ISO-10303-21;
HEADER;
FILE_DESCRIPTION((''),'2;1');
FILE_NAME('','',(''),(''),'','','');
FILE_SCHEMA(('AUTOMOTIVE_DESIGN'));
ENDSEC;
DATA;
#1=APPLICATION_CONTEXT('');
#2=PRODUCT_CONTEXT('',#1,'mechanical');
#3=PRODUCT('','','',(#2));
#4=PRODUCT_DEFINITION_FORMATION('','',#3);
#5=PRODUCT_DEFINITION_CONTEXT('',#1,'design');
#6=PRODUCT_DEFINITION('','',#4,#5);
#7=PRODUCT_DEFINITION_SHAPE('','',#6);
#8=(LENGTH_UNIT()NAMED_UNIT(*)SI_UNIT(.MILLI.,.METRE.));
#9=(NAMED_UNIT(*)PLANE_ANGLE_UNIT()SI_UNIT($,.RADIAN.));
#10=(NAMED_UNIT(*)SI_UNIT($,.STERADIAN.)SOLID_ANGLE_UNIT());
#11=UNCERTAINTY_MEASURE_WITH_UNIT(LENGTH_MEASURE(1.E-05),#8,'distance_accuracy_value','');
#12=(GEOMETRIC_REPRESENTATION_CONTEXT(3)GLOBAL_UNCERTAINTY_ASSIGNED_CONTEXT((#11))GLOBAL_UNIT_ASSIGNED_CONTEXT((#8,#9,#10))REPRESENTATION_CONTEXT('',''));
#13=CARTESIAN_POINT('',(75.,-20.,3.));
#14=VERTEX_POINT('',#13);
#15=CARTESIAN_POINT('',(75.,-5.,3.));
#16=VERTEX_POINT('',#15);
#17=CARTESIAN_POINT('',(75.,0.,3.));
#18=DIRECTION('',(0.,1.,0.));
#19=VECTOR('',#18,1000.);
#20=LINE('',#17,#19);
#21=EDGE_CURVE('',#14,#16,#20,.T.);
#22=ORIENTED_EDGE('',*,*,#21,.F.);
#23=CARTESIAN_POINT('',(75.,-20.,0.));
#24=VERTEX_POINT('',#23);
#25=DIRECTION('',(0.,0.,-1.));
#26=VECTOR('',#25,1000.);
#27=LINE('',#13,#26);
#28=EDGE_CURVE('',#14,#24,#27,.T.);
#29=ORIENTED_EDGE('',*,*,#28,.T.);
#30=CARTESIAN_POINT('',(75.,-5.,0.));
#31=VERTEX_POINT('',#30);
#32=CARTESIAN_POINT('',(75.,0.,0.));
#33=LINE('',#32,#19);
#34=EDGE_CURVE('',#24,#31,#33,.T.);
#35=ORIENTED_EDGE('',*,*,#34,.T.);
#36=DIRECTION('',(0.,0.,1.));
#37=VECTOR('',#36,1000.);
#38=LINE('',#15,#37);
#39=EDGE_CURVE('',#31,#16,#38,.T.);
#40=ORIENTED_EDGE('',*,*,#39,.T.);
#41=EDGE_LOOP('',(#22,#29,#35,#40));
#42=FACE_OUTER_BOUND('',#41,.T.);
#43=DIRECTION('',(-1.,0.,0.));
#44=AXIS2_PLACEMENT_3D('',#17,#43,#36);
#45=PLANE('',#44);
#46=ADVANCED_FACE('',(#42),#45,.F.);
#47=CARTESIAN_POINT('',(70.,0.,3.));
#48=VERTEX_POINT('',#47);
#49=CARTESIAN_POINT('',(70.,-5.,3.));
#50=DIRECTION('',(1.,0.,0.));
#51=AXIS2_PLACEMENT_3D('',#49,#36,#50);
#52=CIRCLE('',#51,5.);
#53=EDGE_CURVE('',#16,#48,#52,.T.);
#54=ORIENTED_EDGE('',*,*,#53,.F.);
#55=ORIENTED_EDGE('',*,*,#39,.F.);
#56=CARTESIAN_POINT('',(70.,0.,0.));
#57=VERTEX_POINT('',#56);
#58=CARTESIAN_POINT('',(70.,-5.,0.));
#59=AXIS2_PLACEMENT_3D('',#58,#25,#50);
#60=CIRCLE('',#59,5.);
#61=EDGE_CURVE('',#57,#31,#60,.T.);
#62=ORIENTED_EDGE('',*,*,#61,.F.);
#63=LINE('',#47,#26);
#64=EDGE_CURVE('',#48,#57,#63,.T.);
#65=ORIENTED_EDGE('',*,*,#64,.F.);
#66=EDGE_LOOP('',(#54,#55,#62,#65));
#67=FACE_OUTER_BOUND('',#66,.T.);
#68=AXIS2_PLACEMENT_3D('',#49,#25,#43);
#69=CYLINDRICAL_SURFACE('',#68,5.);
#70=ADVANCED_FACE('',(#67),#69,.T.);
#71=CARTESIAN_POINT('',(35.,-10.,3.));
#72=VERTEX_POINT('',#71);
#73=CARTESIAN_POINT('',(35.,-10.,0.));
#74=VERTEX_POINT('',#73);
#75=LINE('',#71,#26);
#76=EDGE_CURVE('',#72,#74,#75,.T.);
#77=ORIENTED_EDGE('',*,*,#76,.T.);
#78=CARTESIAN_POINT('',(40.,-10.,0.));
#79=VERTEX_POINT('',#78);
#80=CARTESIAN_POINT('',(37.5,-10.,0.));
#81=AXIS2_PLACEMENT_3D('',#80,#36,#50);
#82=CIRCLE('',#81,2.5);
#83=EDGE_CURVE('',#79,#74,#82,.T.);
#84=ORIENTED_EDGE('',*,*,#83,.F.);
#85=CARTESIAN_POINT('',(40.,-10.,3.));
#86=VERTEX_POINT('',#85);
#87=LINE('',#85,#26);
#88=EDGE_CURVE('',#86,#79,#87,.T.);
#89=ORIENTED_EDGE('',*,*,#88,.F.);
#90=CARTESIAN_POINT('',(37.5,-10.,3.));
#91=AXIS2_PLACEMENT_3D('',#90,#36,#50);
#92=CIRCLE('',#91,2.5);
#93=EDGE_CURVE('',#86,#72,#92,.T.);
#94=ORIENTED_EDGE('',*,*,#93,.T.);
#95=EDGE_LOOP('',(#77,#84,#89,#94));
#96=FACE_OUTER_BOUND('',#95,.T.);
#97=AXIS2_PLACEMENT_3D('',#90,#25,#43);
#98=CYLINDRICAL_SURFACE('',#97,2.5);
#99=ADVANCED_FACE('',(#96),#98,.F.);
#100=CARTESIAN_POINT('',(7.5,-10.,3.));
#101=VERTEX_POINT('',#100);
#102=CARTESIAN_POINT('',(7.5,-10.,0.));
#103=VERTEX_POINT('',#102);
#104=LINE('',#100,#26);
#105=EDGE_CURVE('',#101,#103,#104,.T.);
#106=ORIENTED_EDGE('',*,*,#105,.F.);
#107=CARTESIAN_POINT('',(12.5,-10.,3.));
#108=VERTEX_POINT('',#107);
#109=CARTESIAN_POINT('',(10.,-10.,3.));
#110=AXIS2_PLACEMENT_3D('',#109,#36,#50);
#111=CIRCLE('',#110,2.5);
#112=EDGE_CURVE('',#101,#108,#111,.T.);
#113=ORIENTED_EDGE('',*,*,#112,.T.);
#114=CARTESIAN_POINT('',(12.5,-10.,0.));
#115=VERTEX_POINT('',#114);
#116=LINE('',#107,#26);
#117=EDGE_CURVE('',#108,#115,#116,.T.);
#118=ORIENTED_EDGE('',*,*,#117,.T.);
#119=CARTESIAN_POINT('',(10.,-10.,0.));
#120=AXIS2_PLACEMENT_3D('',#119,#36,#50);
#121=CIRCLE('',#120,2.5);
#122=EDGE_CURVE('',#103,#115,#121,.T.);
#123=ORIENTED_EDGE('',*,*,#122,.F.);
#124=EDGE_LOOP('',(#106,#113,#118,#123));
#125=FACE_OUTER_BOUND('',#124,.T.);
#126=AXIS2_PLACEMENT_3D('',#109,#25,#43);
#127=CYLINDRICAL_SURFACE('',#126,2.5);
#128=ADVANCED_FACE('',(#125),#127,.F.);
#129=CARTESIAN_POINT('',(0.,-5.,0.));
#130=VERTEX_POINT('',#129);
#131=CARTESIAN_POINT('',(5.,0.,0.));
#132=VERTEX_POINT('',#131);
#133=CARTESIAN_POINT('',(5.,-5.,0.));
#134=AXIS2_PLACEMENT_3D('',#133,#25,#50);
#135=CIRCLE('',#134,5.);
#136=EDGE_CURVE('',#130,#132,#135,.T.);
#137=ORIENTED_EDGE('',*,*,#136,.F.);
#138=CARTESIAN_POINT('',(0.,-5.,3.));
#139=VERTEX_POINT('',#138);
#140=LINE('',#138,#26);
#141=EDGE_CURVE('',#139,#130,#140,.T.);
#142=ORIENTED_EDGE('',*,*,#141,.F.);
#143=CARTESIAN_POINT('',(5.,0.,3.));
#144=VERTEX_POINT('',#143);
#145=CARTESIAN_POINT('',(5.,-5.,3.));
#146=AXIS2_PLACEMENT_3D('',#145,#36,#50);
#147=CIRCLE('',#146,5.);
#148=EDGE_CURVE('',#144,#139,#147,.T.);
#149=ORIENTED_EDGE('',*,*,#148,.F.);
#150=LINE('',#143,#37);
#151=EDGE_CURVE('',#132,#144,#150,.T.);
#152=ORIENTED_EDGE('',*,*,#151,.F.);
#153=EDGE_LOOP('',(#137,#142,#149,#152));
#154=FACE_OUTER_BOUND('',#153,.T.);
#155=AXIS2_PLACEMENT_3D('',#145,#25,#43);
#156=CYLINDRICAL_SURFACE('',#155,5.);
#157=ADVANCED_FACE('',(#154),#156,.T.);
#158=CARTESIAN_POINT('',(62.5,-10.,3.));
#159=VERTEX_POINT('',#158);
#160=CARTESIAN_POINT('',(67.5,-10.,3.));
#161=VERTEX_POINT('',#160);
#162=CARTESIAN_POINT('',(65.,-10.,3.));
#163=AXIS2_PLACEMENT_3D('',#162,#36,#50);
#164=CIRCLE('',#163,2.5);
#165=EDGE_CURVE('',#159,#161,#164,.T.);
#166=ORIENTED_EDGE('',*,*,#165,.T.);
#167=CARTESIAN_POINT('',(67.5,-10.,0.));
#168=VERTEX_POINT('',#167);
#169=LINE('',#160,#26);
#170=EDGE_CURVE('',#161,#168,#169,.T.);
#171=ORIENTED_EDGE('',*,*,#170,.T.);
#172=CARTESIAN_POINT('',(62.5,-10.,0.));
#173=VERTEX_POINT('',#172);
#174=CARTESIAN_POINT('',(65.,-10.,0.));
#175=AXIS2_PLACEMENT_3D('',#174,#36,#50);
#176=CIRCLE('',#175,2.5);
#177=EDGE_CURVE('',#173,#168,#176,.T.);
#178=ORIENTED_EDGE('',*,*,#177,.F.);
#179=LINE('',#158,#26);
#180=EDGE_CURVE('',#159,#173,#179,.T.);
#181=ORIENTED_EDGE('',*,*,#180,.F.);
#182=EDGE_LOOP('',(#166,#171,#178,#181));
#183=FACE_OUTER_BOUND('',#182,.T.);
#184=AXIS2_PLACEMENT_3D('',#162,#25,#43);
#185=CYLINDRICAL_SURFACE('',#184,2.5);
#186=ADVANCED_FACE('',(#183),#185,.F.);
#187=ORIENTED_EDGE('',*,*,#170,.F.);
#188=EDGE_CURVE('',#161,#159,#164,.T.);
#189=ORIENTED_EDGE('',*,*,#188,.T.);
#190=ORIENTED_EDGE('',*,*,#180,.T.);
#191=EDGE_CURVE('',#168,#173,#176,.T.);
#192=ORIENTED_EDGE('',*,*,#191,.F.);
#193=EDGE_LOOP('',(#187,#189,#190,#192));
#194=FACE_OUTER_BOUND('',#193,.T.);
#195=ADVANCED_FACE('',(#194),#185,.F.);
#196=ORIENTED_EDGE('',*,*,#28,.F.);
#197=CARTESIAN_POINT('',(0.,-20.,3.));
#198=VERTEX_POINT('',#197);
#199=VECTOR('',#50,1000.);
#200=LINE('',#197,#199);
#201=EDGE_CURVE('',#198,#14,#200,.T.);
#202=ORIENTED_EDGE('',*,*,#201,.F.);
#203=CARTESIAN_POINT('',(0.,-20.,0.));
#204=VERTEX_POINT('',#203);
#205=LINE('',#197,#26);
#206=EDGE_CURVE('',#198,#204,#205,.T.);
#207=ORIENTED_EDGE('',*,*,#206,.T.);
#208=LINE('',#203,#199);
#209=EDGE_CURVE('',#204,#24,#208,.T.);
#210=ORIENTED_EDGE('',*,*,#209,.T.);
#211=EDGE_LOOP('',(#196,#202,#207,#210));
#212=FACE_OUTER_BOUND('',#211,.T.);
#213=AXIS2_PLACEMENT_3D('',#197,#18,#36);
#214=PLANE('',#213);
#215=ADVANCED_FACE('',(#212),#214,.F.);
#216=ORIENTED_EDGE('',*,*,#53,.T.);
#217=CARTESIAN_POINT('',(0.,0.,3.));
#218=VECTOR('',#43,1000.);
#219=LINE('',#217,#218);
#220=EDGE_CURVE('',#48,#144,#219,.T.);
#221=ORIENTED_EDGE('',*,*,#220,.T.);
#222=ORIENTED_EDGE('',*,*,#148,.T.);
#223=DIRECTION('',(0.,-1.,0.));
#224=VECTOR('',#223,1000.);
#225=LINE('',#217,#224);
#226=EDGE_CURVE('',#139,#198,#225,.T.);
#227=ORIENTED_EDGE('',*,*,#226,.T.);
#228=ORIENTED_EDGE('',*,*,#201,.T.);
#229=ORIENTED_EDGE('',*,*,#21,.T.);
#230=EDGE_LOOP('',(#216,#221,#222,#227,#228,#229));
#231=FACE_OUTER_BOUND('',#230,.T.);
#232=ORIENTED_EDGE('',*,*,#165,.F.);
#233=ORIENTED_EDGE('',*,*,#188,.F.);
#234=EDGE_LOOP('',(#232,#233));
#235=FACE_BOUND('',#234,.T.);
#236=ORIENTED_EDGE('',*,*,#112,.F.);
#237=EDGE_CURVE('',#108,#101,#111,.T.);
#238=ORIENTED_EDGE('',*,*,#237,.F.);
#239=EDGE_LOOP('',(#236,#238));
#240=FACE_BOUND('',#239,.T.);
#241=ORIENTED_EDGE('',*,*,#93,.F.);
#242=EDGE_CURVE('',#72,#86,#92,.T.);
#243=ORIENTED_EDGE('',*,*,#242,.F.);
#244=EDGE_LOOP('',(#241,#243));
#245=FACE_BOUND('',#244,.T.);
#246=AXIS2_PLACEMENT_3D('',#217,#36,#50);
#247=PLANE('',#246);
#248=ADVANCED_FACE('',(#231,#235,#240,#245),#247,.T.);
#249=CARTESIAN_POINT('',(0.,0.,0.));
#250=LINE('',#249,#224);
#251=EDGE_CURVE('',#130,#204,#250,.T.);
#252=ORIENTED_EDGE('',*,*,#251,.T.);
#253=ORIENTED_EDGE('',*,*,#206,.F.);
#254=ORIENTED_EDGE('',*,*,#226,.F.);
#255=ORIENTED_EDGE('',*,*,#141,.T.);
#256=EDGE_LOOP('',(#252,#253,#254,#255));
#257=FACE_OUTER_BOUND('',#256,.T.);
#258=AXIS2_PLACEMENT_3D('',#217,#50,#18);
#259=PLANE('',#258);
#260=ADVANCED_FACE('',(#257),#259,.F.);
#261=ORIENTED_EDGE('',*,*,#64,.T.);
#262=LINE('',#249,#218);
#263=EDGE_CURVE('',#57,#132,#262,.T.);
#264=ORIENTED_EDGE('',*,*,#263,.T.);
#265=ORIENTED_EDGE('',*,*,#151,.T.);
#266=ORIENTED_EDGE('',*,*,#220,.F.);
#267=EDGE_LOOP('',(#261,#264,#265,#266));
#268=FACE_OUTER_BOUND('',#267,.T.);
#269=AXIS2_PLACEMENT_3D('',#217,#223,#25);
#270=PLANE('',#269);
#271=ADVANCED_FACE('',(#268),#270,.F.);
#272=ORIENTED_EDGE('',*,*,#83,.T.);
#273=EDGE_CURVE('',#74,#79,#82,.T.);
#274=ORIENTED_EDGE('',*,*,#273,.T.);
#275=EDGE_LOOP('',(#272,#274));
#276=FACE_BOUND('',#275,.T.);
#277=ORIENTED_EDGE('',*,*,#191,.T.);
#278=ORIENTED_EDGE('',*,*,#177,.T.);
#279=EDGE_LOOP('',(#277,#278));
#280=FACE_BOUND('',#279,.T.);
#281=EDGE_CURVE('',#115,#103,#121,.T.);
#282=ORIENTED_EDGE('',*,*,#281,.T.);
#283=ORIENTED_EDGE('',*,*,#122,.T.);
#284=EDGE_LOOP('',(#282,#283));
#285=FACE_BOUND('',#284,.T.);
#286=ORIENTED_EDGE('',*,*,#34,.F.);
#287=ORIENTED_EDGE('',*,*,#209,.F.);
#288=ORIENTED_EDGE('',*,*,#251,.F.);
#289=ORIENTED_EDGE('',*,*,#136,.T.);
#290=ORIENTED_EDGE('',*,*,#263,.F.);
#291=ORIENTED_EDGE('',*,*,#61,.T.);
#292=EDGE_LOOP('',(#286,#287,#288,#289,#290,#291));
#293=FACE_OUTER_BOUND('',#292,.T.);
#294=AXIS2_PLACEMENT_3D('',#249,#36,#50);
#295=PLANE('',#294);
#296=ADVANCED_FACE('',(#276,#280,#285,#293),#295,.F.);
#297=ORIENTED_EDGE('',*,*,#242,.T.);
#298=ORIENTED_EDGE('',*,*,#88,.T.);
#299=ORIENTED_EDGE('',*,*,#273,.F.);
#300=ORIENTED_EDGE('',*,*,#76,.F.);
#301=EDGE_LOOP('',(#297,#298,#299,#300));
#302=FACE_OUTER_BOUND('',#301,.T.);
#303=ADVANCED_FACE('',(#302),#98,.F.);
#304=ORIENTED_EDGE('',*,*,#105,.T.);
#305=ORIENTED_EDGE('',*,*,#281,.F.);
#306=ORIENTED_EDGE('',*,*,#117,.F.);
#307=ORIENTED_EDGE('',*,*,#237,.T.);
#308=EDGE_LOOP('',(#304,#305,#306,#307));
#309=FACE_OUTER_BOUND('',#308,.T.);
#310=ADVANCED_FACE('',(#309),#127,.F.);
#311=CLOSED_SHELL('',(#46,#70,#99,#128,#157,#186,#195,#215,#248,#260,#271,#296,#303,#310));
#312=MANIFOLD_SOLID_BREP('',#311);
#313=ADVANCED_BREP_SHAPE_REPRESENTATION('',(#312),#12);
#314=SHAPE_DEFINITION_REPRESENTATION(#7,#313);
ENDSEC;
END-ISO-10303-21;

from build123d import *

# Parameters (mm, degrees)
SKETCH1_W           = 75
SKETCH1_H           = 20
SKETCH1_R           = 2.5
BOSS_EXTRUDE1_DEPTH = 3
FILLET1_R           = 5


with BuildPart() as part:
    # Sketch1 → Boss-Extrude1 (new body)
    with BuildSketch(Plane.XY):
        with Locations((37.5, -10)):
            Rectangle(SKETCH1_W, SKETCH1_H)
        with Locations((10, -10)):
            Circle(SKETCH1_R, mode=Mode.SUBTRACT)
        with Locations((65, -10)):
            Circle(SKETCH1_R, mode=Mode.SUBTRACT)
        with Locations((37.5, -10)):
            Circle(SKETCH1_R, mode=Mode.SUBTRACT)
    extrude(amount=BOSS_EXTRUDE1_DEPTH)

    # Fillet1
    fillet1_edges = [part.edges().sort_by_distance(p)[0] for p in [
        (0, 0, 1.5),
        (75, 0, 1.5),
    ]]
    fillet(fillet1_edges, radius=FILLET1_R)


solid = part.part
